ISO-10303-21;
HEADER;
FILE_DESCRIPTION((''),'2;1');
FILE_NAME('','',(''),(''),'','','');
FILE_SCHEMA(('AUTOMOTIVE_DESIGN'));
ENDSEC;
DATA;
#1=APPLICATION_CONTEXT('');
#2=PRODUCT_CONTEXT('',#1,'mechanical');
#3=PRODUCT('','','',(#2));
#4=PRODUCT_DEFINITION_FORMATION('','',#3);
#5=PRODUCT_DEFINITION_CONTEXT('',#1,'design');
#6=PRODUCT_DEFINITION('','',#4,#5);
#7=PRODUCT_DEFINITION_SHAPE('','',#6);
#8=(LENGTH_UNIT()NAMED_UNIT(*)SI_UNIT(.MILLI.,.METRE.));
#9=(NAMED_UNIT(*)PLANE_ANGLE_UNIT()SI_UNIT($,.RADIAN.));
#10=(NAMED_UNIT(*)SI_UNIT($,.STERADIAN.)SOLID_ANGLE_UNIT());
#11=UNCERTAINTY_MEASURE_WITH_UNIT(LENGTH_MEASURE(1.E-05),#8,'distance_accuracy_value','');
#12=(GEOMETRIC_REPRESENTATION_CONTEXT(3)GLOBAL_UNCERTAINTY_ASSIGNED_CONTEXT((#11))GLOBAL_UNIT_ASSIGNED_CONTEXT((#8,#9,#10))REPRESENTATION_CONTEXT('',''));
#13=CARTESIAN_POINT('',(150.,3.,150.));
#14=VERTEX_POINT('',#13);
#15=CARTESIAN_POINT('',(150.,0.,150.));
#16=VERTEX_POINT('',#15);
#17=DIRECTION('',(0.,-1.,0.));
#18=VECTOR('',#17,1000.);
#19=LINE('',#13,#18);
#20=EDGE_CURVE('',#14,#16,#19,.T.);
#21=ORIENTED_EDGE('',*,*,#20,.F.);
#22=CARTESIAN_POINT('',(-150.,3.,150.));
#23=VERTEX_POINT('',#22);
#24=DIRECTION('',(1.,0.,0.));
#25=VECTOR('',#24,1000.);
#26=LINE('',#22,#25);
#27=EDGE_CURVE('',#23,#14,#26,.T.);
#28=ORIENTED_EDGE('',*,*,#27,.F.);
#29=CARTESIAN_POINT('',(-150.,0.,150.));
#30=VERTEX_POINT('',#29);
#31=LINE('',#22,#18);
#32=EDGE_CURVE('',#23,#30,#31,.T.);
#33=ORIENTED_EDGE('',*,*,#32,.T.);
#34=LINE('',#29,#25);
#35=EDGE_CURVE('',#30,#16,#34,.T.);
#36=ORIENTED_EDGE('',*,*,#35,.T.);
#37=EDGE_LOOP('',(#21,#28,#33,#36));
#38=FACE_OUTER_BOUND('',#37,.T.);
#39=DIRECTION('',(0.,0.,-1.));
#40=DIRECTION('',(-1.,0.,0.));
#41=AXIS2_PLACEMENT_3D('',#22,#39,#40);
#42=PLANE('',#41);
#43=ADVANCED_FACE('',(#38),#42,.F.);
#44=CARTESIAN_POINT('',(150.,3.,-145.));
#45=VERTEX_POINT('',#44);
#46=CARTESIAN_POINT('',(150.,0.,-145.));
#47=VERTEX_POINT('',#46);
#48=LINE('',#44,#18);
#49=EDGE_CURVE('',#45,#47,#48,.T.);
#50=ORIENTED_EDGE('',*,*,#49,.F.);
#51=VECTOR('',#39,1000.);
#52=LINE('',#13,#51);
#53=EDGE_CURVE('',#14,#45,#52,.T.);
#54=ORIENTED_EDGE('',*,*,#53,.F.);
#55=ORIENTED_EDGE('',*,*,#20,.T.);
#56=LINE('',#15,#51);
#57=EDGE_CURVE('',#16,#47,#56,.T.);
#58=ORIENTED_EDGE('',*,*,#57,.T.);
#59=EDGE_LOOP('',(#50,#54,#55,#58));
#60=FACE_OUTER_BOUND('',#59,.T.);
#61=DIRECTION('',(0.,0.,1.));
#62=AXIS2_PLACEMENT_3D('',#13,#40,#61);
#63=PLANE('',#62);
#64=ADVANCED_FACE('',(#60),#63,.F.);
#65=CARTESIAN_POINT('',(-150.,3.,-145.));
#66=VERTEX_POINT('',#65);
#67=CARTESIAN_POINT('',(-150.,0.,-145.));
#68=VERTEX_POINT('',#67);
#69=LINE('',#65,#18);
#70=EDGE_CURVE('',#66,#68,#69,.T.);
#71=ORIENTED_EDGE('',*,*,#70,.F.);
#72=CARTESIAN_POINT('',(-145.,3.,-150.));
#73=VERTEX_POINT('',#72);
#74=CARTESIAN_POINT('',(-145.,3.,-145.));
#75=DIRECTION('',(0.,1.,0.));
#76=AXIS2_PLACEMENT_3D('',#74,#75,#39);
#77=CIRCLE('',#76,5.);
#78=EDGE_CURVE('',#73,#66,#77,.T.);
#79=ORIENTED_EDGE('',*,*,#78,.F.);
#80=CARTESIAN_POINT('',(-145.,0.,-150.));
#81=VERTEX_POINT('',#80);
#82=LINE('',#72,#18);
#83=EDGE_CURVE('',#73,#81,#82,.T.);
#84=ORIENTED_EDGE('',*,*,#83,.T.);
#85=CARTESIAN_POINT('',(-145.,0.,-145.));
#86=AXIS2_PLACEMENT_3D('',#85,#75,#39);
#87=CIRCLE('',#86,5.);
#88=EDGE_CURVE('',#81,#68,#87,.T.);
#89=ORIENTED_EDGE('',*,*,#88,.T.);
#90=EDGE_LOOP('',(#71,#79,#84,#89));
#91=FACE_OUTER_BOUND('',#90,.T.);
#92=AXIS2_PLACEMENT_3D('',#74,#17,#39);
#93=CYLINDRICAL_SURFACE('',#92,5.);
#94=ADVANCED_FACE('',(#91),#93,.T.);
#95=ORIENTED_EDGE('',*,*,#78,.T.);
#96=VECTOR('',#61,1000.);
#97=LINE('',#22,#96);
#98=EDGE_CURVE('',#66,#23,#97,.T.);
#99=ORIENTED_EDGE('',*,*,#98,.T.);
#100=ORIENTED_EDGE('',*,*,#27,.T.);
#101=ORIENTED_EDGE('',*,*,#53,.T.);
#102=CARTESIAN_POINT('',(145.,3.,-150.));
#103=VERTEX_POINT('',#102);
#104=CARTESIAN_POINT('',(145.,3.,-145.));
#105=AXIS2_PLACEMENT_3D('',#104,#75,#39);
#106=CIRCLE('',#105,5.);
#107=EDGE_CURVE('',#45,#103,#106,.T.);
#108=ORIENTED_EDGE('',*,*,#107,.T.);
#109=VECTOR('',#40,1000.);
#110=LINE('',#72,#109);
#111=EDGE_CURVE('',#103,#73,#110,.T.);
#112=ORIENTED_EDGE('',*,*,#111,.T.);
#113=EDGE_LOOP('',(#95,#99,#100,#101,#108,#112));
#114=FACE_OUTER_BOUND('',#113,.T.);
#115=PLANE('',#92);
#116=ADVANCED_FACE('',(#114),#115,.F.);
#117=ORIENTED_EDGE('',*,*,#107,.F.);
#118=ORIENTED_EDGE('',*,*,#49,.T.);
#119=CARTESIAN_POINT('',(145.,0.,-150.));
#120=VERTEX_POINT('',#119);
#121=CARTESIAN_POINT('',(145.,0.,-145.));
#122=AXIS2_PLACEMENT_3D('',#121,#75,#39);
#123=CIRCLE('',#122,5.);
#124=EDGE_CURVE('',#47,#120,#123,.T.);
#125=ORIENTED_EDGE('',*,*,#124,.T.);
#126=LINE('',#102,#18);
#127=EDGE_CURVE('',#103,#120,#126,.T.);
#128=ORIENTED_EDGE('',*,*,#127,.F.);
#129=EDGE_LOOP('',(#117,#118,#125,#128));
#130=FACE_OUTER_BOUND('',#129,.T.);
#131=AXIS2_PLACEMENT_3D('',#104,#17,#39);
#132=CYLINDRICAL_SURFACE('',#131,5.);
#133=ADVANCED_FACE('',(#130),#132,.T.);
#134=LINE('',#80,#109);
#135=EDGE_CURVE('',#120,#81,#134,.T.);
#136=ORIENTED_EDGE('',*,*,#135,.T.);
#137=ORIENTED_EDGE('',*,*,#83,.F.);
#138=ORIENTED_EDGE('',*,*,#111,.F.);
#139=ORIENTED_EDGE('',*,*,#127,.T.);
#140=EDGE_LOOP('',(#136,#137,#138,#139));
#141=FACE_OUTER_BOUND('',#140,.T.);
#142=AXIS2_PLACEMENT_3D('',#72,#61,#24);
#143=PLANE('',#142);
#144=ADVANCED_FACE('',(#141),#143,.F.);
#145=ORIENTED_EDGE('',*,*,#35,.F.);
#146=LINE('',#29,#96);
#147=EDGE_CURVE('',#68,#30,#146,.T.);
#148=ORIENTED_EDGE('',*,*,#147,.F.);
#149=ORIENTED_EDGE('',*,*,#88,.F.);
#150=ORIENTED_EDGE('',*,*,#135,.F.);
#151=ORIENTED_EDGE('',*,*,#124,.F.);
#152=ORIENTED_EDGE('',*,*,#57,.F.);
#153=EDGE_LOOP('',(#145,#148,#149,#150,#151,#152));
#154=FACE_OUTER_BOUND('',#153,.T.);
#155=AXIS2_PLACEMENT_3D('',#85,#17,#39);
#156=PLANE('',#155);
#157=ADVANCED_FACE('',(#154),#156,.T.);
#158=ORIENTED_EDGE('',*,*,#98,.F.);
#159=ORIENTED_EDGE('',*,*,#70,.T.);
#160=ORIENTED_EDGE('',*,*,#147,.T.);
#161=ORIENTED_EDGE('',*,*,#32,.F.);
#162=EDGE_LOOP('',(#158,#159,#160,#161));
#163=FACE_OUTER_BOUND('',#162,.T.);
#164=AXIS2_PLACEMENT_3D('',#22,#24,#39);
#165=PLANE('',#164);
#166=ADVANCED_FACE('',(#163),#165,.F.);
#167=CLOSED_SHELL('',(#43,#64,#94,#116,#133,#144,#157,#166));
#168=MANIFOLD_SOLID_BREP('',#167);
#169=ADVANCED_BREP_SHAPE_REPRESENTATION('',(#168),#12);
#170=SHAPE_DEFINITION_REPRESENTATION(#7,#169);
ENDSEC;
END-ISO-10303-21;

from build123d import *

# Parameters (mm, degrees)
BOSS_EXTRUDE1_DEPTH = 3


with BuildPart() as part:
    # Sketch1 → Boss-Extrude1 (new body)
    with BuildSketch(Plane(origin=(0, 0, 0), x_dir=(1, 0, 0), z_dir=(0, 1, 0))):
        with BuildLine():
            Line((-150, -150), (150, -150))
            Line((150, -150), (150, 145))
            ThreePointArc((150, 145), (148.535533906, 148.535533906), (145, 150))
            Line((145, 150), (-145, 150))
            ThreePointArc((-145, 150), (-148.535533906, 148.535533906), (-150, 145))
            Line((-150, 145), (-150, -150))
        make_face()
    extrude(amount=BOSS_EXTRUDE1_DEPTH)


solid = part.part
